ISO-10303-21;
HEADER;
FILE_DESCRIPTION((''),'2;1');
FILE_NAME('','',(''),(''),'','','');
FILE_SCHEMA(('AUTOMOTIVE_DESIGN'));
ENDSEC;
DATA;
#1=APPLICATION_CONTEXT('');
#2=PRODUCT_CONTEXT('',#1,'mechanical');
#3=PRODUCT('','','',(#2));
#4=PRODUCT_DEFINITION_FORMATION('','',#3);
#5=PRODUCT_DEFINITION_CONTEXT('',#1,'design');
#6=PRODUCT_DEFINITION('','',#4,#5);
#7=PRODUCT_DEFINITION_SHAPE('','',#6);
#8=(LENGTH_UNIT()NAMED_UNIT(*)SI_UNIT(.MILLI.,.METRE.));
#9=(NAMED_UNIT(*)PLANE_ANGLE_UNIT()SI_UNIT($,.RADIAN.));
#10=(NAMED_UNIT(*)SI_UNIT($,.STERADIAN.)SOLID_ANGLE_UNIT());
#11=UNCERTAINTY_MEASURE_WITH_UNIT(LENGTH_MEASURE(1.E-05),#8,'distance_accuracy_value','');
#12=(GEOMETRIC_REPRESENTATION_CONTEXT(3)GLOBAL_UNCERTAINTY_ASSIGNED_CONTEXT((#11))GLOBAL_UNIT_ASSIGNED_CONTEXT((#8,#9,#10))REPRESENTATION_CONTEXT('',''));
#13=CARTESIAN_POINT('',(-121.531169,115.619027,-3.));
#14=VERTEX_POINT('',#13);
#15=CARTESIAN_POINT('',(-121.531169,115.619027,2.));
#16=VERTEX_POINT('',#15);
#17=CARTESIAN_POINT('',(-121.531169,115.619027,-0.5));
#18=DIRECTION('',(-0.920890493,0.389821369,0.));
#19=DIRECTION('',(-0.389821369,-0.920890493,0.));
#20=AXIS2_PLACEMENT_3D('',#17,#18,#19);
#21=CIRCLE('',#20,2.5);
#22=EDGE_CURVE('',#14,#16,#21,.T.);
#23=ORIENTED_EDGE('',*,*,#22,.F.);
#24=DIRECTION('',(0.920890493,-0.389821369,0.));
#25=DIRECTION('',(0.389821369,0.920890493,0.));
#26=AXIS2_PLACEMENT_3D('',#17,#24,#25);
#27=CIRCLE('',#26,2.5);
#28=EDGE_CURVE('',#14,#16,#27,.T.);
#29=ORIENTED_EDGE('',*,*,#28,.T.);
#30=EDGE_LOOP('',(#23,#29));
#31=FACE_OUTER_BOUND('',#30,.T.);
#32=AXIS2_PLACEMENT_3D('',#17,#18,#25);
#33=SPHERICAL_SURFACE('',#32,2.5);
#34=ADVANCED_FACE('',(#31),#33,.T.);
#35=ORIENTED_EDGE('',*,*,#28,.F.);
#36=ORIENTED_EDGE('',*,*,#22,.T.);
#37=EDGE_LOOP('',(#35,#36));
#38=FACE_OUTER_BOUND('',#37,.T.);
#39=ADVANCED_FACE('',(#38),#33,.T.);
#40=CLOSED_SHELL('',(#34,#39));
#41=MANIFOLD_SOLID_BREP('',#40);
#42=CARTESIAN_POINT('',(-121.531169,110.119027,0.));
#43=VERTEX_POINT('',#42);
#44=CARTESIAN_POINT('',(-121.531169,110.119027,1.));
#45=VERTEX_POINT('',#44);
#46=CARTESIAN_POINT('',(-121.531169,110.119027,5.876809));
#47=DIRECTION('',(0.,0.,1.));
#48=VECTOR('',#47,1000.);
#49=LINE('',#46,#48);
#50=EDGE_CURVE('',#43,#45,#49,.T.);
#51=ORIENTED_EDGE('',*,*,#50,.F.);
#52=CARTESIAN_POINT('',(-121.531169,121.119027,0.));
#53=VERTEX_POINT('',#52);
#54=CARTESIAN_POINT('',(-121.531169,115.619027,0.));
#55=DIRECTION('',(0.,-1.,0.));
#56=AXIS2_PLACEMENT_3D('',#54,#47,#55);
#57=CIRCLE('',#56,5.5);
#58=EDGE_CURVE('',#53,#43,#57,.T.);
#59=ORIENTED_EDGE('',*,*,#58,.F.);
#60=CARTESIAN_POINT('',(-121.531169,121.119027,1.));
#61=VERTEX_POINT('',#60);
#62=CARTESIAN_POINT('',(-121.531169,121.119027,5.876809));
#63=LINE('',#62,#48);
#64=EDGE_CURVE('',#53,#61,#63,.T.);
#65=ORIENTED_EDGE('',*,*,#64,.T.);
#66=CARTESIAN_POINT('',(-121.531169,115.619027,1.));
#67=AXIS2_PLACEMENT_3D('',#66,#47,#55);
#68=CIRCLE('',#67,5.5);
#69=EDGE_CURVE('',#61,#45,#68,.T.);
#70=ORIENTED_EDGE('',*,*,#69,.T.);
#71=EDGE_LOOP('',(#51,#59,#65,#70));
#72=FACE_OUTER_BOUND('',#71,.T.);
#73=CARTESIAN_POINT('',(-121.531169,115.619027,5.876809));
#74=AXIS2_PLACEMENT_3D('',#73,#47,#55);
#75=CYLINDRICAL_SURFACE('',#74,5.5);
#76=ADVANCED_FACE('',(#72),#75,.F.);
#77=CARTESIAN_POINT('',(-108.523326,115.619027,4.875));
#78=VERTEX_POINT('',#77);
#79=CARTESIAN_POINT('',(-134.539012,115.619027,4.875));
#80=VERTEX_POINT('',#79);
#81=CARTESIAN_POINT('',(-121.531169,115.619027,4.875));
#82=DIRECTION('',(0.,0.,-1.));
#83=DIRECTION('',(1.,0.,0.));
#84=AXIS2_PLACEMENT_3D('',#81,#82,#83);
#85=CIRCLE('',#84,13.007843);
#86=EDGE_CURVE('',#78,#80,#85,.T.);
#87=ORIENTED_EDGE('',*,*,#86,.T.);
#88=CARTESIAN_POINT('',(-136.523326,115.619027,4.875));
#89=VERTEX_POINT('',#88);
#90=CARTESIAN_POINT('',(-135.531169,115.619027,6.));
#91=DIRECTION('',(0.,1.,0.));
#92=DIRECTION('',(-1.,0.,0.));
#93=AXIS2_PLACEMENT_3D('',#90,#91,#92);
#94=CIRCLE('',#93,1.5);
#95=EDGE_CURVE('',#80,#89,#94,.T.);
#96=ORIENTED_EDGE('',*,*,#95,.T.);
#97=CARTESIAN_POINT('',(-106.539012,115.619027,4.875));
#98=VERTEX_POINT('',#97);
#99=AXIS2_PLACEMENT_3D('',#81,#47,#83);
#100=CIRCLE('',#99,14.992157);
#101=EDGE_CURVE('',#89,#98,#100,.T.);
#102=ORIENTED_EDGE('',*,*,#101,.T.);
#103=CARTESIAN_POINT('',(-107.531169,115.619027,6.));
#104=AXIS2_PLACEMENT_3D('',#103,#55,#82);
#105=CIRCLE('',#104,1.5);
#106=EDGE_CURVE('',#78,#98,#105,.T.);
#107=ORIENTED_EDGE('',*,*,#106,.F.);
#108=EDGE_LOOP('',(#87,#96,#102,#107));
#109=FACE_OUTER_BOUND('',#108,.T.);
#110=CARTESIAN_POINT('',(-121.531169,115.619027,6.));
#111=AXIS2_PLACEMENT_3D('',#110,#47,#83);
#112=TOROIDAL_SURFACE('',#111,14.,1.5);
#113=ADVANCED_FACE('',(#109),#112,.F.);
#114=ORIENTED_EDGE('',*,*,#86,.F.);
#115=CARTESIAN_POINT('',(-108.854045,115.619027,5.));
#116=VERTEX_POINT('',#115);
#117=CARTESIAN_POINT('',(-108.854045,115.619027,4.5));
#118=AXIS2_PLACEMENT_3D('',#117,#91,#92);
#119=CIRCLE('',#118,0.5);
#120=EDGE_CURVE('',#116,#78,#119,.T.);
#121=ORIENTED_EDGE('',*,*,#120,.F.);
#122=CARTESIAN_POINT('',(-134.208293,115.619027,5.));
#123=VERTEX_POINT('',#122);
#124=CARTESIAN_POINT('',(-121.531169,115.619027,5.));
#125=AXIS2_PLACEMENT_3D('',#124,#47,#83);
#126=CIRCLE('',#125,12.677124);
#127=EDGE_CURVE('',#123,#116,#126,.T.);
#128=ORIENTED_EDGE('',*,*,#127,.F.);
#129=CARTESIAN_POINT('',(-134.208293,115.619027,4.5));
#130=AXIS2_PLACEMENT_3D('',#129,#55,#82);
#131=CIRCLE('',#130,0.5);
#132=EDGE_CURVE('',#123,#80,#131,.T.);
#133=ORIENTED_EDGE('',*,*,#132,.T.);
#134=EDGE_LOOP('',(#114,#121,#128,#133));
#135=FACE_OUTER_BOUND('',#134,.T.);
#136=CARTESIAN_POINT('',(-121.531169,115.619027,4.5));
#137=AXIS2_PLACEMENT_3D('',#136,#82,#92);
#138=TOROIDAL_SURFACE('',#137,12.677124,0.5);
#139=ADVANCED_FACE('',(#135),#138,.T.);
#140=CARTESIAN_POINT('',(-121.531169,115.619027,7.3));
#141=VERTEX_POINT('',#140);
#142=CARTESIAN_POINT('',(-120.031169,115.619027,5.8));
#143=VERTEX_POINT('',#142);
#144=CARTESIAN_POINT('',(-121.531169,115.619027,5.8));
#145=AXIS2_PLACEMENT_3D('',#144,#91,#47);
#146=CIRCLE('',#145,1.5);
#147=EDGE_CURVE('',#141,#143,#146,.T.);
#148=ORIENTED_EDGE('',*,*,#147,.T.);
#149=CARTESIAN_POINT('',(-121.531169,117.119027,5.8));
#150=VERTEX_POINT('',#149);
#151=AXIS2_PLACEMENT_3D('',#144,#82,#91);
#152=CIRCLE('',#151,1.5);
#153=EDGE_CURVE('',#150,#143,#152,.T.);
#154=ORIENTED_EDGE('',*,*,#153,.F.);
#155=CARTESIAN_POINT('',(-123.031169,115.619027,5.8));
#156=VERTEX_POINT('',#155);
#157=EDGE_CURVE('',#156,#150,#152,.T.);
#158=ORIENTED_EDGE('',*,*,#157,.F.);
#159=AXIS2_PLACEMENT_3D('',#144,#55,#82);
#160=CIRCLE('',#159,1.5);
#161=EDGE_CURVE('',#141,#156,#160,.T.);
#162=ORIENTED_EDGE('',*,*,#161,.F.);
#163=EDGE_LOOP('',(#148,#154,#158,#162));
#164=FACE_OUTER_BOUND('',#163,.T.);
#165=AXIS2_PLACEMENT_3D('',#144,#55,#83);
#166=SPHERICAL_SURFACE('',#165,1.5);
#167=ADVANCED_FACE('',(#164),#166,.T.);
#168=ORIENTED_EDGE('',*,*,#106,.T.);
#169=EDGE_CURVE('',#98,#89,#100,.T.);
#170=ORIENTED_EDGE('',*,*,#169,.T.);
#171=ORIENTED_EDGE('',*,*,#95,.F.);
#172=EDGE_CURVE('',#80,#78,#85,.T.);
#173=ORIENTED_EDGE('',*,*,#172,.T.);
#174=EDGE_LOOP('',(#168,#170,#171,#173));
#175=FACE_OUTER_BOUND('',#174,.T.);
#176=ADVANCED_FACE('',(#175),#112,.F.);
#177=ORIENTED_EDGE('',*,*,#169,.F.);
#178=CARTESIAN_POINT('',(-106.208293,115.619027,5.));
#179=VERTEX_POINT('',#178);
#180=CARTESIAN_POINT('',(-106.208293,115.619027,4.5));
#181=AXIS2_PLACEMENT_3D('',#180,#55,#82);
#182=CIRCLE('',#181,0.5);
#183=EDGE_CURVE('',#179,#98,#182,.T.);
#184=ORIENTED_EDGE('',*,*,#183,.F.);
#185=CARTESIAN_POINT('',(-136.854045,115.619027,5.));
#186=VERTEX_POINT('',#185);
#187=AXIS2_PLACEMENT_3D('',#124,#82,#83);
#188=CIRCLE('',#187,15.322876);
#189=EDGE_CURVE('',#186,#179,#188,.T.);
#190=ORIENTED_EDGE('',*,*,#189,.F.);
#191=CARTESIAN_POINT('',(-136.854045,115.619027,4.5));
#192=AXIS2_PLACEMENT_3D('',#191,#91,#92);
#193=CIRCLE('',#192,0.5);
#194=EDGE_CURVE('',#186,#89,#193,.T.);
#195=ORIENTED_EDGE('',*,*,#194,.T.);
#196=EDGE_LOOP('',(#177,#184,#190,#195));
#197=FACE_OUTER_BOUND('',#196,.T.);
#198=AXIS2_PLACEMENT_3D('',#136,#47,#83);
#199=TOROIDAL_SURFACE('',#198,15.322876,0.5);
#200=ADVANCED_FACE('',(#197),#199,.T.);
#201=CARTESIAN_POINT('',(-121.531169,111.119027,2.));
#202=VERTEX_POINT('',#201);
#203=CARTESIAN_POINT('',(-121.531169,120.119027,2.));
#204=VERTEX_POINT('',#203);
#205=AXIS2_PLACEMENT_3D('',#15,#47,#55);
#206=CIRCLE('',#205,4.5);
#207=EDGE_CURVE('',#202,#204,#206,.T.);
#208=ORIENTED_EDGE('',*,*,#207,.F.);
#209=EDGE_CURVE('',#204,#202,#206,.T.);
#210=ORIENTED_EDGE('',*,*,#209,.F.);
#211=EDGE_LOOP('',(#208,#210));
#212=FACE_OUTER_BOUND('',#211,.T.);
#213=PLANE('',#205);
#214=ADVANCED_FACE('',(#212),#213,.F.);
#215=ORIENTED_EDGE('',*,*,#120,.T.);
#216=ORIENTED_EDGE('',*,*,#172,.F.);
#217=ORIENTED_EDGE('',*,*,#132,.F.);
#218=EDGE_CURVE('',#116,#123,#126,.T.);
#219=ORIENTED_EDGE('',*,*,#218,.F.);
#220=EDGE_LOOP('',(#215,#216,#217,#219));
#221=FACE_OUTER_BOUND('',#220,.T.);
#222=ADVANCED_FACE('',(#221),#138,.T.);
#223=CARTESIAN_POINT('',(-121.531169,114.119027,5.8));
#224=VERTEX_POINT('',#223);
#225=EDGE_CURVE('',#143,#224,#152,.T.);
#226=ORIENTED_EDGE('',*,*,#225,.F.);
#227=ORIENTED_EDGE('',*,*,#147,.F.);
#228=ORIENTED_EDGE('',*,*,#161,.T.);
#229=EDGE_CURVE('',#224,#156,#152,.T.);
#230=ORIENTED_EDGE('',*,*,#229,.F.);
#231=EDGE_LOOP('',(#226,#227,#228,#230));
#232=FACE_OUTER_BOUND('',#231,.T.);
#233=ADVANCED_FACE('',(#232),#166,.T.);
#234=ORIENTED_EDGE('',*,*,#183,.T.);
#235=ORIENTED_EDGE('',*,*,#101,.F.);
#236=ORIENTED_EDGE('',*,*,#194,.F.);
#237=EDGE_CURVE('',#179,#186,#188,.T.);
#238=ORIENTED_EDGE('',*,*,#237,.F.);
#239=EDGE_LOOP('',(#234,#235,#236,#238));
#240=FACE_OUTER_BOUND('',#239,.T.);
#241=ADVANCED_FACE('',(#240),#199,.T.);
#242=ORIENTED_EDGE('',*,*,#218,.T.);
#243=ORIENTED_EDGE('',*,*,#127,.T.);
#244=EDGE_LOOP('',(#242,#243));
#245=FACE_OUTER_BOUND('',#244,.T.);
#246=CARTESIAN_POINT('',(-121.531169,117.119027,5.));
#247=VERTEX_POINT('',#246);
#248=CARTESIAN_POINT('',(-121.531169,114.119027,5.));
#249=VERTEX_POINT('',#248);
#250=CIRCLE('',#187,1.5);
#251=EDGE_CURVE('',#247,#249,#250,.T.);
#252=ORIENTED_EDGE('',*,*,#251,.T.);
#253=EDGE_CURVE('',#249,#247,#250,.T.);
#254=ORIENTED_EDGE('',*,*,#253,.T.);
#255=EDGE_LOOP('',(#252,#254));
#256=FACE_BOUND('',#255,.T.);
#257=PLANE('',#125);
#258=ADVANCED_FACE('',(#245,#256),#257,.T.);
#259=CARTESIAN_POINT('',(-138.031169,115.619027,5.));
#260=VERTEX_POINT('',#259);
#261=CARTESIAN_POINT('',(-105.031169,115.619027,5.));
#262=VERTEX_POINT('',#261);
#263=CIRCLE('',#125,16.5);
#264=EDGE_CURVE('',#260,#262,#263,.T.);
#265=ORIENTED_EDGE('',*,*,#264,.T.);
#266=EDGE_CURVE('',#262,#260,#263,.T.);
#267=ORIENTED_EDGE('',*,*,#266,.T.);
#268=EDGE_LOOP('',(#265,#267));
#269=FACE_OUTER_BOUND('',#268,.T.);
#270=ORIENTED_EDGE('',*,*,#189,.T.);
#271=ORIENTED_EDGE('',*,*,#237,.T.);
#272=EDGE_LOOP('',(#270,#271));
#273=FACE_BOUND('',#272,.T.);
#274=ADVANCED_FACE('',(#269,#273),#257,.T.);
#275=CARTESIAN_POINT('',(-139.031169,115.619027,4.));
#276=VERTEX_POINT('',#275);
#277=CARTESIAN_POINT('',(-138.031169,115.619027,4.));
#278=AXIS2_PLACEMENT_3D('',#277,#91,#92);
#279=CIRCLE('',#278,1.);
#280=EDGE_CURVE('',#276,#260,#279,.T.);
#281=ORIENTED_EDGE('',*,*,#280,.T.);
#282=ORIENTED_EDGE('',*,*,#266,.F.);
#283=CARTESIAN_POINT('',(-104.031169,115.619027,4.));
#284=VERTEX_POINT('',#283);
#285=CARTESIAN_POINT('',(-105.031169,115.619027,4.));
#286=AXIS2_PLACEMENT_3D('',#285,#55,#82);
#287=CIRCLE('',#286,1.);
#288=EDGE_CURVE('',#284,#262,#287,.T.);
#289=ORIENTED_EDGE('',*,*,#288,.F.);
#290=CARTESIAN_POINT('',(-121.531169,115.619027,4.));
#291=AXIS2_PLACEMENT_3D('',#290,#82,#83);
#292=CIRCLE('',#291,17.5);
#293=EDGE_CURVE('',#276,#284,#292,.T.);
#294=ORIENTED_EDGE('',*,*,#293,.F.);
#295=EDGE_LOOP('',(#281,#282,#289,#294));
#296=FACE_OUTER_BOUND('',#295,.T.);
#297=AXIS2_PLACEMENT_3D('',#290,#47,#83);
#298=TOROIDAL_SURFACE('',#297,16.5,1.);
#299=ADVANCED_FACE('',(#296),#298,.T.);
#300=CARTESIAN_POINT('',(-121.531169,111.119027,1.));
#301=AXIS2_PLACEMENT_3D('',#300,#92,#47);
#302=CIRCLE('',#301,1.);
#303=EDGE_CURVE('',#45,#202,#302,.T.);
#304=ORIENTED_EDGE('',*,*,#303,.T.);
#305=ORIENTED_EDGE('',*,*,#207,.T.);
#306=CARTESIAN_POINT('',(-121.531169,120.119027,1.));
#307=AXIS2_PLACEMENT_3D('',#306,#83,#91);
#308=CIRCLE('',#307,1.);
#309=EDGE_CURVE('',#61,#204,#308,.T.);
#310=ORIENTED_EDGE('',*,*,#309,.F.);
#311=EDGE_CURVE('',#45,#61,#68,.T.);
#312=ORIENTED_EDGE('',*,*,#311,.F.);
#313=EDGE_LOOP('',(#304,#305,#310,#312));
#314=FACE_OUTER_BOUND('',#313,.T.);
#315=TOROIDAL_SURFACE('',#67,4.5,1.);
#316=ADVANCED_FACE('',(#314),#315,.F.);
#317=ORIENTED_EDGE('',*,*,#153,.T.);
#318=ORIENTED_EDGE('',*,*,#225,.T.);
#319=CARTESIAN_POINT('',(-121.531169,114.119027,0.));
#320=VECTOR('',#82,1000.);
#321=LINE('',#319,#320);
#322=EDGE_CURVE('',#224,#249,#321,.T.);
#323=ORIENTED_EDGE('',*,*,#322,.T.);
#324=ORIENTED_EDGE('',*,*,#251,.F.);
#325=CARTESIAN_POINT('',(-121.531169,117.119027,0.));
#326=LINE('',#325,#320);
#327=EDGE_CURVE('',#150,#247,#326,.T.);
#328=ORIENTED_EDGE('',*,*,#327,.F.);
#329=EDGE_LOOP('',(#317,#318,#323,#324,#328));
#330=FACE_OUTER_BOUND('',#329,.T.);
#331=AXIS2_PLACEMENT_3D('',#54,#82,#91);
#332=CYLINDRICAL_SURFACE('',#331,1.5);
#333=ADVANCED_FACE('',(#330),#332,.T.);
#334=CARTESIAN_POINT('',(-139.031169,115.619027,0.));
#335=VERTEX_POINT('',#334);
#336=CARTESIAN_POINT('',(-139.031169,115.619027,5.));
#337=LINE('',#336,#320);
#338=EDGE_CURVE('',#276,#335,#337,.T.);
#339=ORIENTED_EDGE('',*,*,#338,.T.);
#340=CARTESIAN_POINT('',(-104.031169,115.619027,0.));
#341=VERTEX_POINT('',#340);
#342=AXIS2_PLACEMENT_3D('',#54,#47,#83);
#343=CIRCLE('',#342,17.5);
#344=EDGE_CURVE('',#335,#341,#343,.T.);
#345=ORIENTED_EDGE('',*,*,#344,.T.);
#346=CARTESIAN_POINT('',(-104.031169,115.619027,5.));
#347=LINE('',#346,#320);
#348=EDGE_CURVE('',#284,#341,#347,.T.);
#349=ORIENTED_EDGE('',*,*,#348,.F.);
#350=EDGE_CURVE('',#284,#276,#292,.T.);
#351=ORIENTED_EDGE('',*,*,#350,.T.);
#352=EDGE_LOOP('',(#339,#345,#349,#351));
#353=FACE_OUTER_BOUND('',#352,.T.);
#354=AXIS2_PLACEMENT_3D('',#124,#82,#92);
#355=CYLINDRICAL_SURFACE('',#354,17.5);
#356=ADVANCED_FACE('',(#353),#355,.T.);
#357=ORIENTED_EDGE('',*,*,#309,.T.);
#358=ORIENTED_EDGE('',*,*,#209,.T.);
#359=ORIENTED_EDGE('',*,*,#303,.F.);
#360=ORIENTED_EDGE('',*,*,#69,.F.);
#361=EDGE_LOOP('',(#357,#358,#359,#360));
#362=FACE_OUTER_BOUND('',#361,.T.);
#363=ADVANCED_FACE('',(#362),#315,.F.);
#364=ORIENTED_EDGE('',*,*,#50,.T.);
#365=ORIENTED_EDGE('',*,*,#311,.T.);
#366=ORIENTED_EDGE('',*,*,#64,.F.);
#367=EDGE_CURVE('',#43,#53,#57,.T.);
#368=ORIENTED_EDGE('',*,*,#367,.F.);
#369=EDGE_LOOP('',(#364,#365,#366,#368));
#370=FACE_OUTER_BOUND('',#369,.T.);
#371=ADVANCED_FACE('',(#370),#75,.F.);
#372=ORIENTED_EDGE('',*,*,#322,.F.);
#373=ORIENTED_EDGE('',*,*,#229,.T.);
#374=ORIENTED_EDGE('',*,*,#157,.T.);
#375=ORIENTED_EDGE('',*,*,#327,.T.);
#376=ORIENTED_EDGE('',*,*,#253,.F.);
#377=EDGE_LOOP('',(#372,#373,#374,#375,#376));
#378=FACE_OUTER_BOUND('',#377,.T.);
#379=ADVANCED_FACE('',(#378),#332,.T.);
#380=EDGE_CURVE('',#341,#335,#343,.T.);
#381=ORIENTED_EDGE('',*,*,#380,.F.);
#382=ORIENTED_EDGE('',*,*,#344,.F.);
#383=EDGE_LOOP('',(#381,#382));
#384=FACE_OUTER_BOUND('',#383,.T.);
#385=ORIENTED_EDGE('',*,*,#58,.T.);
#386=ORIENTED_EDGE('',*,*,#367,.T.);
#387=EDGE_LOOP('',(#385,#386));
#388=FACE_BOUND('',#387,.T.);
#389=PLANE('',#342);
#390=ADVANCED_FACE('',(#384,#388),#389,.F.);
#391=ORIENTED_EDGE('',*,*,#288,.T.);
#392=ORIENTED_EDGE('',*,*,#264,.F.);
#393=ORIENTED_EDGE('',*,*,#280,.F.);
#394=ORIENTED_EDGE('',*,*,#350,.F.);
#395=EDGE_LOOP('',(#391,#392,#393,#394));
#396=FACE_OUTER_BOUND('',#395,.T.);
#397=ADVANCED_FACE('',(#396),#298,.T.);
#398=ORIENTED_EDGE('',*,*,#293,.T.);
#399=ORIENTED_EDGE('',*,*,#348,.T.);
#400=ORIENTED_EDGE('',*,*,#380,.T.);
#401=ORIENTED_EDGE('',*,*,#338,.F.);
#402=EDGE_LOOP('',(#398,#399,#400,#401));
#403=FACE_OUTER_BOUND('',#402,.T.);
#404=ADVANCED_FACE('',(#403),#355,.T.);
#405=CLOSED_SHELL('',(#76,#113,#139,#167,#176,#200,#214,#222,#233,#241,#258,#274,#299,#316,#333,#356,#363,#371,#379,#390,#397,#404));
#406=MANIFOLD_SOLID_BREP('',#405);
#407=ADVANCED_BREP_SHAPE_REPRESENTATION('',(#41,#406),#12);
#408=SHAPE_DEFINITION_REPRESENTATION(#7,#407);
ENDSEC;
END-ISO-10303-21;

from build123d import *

# Parameters (mm, degrees)
SKETCH1_R           = 17.5
BOSS_EXTRUDE1_DEPTH = 5
SKETCH5_R           = 1.5
FILLET1_R           = 1
FILLET2_R           = 0.5


with BuildPart() as part:
    # Sketch1 → Boss-Extrude1 (new body)
    with BuildSketch(Plane.XY):
        with Locations((-121.531169153, 115.619026916)):
            Circle(SKETCH1_R)
    extrude(amount=BOSS_EXTRUDE1_DEPTH)

    # Sketch2 → Cut-Revolve1 (revolve, cut)
    with BuildSketch(Plane(origin=(-144.568448824, 61.197146719, 0), x_dir=(-0.38982136890031954, -0.9208904931362258, 0), z_dir=(0.9208904931362258, -0.38982136890031954, 0)), mode=Mode.PRIVATE) as cut_revolve1_sk:
        with BuildLine():
            Line((-59.097015989, 0), (-53.597015989, 0))
            Line((-53.597015989, 0), (-53.597015989, -1))
            ThreePointArc((-53.597015989, -1), (-53.889909208, -1.707106781), (-54.597015989, -2))
            Line((-54.597015989, -2), (-59.097015989, -2))
            Line((-59.097015989, -2), (-59.097015989, 0))
        make_face()
    revolve(cut_revolve1_sk.sketch.rotate(Axis((-121.531169153, 115.619026916, 5.87680908), (0, 0, -1)), 337.056615089), axis=Axis((-121.531169153, 115.619026916, 5.87680908), (0, 0, -1)), mode=Mode.SUBTRACT)

    # Sketch5 → Cut-Revolve2 (revolve, cut)
    with BuildSketch(Plane.ZX.offset(115.619026916), mode=Mode.PRIVATE) as cut_revolve2_sk:
        with Locations((6, -107.531169153)):
            Circle(SKETCH5_R)
    revolve(cut_revolve2_sk.sketch.rotate(Axis((-121.531169153, 115.619026916, 5), (0, 0, -1)), 292.943384911), axis=Axis((-121.531169153, 115.619026916, 5), (0, 0, -1)), mode=Mode.SUBTRACT)

    # Fillet1
    fillet1_edges = [part.edges().sort_by_distance(p)[0] for p in [
        (-139.031169153, 115.619026916, 5),
    ]]
    fillet(fillet1_edges, radius=FILLET1_R)

    # Fillet2
    fillet2_edges = [part.edges().sort_by_distance(p)[0] for p in [
        (-126.552834778, 103.756146884, 5),
        (-127.424501858, 101.696973141, 5),
    ]]
    fillet(fillet2_edges, radius=FILLET2_R)

    # Sketch6 → Revolve2 (revolve)
    with BuildSketch(Plane.ZX.offset(115.619026916)):
        with BuildLine():
            Line((5.8, -120.031169153), (4, -120.031169153))
            Line((4, -120.031169153), (4, -121.531169153))
            Line((4, -121.531169153), (7.3, -121.531169153))
            ThreePointArc((7.3, -121.531169153), (6.860660172, -120.470508981), (5.8, -120.031169153))
        make_face()
    revolve(axis=Axis((-121.531169153, 115.619026916, 0), (0, 0, 1)))


with BuildPart() as body_2:
    # Sketch4 → Revolve1 (revolve)
    with BuildSketch(Plane(origin=(-144.568448824, 61.197146719, 0), x_dir=(-0.38982136890031954, -0.9208904931362258, 0), z_dir=(0.9208904931362258, -0.38982136890031954, 0))):
        with BuildLine():
            Line((-59.097015989, -2), (-59.097015989, 3))
            ThreePointArc((-59.097015989, 3), (-56.597015989, 0.5), (-59.097015989, -2))
        make_face()
    revolve(axis=Axis((-121.531169153, 115.619026916, 5), (0, 0, -1)))


solid = Compound([part.part, body_2.part])
